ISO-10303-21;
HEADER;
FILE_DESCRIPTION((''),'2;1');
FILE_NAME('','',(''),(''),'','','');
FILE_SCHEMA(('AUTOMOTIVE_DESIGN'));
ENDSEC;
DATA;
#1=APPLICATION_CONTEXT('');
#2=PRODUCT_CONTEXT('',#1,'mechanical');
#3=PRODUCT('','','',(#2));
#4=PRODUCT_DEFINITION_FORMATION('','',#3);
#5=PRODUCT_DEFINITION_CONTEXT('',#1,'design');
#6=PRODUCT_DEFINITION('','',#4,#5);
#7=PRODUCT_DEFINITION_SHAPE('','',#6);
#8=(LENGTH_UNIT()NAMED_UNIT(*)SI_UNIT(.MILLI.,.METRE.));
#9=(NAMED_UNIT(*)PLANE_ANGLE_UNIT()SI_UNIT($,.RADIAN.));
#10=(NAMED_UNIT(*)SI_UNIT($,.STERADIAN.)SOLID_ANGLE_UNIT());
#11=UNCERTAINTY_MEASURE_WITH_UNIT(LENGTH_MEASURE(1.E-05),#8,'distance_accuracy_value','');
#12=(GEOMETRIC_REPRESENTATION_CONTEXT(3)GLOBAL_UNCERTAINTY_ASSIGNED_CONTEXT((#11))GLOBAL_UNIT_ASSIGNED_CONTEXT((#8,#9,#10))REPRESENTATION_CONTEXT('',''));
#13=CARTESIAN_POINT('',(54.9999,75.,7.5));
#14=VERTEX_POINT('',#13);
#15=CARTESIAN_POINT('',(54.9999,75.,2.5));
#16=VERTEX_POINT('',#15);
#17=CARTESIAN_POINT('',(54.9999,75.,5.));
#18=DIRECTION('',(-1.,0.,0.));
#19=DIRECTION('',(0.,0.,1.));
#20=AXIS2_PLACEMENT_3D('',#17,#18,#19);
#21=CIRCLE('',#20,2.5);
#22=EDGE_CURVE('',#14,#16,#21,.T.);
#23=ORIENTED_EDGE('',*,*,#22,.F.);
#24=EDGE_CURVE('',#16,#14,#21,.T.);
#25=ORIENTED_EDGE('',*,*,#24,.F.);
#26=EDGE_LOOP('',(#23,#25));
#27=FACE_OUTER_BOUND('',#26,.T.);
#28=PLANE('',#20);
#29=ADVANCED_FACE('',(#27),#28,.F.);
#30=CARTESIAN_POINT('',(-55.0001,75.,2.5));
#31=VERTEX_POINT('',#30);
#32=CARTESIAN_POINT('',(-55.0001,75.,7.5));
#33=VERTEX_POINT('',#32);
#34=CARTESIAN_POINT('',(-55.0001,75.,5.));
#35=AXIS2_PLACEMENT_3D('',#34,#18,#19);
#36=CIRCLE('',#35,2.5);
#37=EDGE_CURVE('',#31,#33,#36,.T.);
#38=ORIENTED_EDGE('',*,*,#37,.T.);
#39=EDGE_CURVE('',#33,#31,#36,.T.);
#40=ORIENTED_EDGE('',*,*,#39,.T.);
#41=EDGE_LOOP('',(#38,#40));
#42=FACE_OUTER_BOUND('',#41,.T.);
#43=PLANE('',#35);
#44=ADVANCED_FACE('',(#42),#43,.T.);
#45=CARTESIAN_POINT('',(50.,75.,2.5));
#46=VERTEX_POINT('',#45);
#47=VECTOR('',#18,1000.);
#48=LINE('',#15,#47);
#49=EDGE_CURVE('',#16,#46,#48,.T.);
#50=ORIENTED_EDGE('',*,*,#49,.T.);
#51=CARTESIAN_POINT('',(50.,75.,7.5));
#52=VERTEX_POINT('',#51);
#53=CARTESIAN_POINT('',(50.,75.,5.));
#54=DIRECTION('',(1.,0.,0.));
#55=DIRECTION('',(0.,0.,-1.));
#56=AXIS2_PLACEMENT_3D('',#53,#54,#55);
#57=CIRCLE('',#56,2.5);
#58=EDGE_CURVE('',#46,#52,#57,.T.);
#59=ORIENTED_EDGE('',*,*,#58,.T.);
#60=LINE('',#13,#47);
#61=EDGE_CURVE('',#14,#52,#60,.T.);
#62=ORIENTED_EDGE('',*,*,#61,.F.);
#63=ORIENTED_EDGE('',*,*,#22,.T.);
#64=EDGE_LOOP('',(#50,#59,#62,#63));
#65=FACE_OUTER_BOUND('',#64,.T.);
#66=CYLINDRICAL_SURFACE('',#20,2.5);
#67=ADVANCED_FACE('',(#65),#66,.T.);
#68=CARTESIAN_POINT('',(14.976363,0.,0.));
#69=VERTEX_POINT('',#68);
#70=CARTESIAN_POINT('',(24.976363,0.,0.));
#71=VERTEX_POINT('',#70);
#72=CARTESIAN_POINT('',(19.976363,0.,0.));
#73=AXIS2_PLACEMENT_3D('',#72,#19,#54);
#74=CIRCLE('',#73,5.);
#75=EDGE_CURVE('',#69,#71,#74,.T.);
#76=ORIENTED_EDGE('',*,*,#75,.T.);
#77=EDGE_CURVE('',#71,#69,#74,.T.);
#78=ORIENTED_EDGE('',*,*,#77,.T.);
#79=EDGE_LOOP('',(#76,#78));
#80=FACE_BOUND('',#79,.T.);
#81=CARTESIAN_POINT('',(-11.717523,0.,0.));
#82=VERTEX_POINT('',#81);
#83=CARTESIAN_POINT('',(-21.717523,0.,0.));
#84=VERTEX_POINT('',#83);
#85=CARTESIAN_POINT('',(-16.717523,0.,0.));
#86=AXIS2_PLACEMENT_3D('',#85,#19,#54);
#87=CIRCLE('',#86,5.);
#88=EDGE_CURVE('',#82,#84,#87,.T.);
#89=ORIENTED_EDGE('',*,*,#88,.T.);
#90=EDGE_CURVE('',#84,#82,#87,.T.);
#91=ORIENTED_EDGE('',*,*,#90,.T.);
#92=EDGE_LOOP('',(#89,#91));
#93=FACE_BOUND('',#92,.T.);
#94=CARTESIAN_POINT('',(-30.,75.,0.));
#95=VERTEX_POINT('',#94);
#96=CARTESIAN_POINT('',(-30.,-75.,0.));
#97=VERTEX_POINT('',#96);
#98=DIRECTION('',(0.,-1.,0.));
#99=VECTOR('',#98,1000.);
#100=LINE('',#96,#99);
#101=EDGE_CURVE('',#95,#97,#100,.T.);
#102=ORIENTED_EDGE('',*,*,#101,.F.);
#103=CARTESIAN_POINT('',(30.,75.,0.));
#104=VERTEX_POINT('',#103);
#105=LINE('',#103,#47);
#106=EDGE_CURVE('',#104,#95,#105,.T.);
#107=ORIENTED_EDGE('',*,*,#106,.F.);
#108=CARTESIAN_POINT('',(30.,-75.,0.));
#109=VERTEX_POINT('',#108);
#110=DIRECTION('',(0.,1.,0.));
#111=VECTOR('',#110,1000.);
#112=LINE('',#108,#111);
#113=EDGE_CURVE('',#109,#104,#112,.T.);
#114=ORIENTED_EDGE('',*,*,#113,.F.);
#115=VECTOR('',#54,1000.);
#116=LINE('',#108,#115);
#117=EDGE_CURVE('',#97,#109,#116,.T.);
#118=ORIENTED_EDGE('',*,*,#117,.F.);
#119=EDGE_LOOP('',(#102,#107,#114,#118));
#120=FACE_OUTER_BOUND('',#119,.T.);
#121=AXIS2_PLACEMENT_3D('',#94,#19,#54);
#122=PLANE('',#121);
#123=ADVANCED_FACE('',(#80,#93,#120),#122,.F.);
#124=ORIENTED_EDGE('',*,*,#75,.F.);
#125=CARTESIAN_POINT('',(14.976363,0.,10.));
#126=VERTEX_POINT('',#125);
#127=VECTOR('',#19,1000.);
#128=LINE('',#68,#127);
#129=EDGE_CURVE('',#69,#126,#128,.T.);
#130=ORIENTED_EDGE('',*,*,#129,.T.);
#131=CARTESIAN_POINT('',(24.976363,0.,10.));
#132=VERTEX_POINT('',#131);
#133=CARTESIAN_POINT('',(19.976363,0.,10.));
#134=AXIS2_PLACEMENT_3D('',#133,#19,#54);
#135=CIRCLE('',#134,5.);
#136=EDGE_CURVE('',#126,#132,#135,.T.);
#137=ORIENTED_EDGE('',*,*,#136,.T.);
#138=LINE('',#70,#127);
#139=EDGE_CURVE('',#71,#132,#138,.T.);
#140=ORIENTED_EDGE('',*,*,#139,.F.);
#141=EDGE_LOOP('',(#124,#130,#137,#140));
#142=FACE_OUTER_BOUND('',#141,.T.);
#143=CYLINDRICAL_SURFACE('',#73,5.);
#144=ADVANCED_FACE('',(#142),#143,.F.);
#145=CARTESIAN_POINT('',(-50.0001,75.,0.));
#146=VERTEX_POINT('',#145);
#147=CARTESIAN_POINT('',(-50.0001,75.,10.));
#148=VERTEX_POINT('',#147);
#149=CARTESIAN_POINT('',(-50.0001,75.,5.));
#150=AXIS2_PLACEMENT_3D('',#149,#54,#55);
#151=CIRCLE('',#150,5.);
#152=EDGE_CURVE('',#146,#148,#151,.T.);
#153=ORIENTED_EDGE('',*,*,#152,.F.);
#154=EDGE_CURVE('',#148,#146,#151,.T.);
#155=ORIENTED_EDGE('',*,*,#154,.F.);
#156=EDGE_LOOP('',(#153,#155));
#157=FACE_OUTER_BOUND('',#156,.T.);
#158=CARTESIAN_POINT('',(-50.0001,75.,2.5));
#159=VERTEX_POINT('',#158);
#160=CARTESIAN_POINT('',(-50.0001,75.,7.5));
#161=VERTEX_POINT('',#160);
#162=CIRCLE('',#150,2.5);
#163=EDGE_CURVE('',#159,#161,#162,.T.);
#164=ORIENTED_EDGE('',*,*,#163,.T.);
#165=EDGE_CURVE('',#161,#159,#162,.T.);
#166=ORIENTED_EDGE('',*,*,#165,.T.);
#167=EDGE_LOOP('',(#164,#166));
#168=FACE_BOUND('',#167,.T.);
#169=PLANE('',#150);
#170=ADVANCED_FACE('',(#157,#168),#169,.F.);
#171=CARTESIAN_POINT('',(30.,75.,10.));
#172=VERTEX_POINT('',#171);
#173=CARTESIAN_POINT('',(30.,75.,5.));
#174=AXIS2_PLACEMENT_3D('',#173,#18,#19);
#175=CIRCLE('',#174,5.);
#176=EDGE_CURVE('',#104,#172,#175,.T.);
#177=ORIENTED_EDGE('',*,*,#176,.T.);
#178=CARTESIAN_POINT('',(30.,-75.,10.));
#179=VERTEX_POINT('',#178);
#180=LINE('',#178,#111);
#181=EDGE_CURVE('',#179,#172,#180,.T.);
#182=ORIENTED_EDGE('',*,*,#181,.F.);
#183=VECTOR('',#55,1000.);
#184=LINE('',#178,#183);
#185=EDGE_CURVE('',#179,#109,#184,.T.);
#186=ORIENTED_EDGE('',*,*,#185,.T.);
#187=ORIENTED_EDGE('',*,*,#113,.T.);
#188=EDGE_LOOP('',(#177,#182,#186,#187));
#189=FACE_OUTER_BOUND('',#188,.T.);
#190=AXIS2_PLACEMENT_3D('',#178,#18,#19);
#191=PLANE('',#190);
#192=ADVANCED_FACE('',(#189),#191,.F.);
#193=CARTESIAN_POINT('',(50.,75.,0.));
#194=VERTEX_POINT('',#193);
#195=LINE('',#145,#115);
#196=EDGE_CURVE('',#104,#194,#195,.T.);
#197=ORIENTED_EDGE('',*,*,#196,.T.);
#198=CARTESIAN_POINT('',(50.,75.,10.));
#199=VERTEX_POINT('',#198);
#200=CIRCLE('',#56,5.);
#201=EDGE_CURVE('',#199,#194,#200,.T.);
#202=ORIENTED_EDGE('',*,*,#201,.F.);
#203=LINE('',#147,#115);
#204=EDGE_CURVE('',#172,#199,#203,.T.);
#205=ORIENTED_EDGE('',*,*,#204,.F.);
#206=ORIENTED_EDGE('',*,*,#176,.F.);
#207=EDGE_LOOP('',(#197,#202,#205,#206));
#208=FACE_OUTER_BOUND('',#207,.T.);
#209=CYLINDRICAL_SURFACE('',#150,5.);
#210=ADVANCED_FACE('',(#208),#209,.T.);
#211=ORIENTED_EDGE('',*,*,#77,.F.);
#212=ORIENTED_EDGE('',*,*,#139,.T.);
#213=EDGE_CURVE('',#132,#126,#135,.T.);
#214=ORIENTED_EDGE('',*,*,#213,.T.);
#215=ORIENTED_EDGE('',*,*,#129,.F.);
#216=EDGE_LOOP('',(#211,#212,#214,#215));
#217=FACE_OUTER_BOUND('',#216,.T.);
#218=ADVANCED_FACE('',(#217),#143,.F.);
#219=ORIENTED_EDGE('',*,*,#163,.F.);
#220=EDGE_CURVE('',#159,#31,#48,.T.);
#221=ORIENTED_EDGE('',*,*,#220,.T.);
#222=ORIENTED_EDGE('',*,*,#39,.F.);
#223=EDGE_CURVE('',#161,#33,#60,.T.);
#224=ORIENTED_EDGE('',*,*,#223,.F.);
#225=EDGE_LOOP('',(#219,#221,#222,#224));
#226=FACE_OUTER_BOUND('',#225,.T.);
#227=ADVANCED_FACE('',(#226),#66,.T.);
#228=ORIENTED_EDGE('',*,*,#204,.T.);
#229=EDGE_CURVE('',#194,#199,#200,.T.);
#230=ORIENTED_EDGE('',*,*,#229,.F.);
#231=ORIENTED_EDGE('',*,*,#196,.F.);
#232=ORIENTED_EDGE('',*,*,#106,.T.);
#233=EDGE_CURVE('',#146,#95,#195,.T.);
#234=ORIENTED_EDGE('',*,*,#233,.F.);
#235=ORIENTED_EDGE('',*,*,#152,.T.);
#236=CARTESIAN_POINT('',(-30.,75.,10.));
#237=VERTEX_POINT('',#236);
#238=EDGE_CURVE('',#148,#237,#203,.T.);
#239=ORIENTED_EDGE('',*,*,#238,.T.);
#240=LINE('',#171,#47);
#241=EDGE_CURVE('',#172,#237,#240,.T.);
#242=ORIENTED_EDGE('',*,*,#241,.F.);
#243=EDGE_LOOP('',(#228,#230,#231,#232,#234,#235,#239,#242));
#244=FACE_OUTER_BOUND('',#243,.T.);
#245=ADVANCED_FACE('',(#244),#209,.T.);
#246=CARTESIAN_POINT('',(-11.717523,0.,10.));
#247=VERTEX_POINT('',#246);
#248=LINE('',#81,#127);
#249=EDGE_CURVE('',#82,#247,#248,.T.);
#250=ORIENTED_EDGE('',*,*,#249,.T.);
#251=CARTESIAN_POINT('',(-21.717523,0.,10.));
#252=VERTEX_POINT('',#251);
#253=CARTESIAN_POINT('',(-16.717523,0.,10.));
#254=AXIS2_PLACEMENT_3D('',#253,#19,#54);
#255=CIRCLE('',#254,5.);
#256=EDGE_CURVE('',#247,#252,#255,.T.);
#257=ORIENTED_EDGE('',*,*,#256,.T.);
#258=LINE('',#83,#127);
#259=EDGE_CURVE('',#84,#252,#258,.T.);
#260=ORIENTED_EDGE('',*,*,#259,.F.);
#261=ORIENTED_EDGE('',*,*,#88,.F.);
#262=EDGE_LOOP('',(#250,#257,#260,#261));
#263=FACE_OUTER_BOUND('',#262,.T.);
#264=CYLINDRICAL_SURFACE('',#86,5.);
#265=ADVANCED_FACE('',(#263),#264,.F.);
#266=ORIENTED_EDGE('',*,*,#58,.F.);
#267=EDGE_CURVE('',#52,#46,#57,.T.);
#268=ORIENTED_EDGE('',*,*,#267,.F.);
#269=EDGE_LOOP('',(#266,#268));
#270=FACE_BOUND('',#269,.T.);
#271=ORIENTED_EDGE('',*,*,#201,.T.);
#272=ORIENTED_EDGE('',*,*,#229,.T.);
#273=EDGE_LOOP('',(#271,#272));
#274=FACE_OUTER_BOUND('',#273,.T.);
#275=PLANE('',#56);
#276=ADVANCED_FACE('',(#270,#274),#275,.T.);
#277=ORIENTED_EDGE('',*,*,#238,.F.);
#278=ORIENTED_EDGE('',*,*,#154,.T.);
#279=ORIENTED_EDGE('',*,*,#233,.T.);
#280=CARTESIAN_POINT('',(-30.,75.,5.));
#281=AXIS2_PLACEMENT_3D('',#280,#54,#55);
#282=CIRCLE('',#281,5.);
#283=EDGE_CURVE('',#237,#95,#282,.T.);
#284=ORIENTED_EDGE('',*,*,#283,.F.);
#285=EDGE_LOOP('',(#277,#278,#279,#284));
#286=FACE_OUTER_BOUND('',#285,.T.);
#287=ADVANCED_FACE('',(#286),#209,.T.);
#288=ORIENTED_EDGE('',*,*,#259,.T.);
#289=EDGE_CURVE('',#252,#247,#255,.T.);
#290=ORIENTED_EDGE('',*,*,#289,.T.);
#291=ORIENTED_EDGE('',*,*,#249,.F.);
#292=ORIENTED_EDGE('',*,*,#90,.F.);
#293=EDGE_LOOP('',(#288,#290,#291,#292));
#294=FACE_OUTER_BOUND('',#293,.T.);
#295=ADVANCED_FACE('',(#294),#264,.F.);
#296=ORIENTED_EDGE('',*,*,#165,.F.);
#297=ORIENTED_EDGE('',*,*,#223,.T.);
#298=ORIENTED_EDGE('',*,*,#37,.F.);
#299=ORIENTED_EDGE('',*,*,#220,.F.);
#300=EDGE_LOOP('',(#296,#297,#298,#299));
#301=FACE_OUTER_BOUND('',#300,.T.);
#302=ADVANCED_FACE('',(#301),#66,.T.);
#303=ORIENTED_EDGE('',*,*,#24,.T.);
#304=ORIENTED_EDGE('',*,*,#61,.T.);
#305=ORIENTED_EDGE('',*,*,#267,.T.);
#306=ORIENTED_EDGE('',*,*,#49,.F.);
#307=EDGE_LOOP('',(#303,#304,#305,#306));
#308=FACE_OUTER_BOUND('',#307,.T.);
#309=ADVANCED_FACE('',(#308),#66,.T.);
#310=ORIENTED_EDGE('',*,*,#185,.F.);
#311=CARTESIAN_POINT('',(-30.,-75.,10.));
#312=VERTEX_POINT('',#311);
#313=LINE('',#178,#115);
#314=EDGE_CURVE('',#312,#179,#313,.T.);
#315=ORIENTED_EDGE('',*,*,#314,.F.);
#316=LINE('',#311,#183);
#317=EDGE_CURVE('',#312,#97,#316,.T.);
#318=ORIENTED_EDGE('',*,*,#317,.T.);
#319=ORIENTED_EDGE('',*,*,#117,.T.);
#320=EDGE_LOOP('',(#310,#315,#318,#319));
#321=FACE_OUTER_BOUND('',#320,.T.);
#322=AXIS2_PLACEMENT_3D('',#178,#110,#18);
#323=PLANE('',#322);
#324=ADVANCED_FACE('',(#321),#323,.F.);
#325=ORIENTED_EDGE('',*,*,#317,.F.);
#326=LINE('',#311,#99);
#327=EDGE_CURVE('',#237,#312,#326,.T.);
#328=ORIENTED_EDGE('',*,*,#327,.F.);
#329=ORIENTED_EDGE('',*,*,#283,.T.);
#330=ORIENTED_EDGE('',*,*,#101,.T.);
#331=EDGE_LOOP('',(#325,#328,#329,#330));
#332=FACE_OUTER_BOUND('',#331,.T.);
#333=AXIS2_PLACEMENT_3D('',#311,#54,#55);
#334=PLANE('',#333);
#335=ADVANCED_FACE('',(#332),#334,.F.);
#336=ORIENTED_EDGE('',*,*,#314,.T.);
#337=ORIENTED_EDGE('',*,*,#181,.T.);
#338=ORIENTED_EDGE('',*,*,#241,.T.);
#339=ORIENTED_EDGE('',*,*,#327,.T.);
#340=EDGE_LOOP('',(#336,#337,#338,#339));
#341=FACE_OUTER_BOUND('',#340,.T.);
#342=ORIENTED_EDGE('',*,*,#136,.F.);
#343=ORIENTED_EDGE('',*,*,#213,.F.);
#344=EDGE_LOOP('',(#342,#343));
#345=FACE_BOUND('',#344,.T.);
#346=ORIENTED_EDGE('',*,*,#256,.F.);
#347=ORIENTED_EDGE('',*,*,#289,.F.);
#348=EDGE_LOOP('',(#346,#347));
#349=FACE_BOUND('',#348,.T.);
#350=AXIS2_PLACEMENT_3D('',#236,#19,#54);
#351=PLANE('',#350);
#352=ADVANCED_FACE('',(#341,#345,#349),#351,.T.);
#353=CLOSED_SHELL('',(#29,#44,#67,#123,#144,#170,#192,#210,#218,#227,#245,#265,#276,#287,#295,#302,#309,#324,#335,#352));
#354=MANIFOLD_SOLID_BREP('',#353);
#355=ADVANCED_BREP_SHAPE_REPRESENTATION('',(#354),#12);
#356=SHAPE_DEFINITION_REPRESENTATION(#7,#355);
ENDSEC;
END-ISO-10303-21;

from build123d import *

# Parameters (mm, degrees)
SKETCH1_W                = 60
SKETCH1_H                = 150
BOSS_EXTRUDE1_DEPTH      = 10
SKETCH2_R                = 5
CUT_EXTRUDE1_DEPTH       = 10
BOSS_EXTRUDE2_DEPTH      = 20
BOSS_EXTRUDE2_DEPTH_BACK = 80.0001
SKETCH3_R                = 5
BOSS_EXTRUDE3_DEPTH      = 5
BOSS_EXTRUDE3_DEPTH_BACK = 105
SKETCH4_R                = 2.5


with BuildPart() as part:
    # Sketch1 → Boss-Extrude1 (new body)
    with BuildSketch(Plane.XY):
        Rectangle(SKETCH1_W, SKETCH1_H)
    extrude(amount=BOSS_EXTRUDE1_DEPTH)

    # Sketch2 → Cut-Extrude1 (cut)
    with BuildSketch(Plane.XY.offset(10)):
        with Locations((-16.71752283, 0)):
            Circle(SKETCH2_R)
        with Locations((19.976362571, 0)):
            Circle(SKETCH2_R)
    extrude(amount=-CUT_EXTRUDE1_DEPTH, mode=Mode.SUBTRACT)

    # Sketch3 → Boss-Extrude2 (add, two sides: drawn at the far end of the back side and taken through both)
    with BuildSketch(Plane(origin=(30, 0, 0), x_dir=(0, 0, -1), z_dir=(1, 0, 0)).offset(-BOSS_EXTRUDE2_DEPTH_BACK)):
        with Locations((-5, 75)):
            Circle(SKETCH3_R)
    extrude(amount=BOSS_EXTRUDE2_DEPTH + BOSS_EXTRUDE2_DEPTH_BACK)

    # Sketch4 → Boss-Extrude3 (add, two sides: drawn at the far end of the back side and taken through both)
    with BuildSketch(Plane.ZY.offset(50.0001).offset(-BOSS_EXTRUDE3_DEPTH_BACK)):
        with Locations((5, 75)):
            Circle(SKETCH4_R)
    extrude(amount=BOSS_EXTRUDE3_DEPTH + BOSS_EXTRUDE3_DEPTH_BACK)


solid = part.part
